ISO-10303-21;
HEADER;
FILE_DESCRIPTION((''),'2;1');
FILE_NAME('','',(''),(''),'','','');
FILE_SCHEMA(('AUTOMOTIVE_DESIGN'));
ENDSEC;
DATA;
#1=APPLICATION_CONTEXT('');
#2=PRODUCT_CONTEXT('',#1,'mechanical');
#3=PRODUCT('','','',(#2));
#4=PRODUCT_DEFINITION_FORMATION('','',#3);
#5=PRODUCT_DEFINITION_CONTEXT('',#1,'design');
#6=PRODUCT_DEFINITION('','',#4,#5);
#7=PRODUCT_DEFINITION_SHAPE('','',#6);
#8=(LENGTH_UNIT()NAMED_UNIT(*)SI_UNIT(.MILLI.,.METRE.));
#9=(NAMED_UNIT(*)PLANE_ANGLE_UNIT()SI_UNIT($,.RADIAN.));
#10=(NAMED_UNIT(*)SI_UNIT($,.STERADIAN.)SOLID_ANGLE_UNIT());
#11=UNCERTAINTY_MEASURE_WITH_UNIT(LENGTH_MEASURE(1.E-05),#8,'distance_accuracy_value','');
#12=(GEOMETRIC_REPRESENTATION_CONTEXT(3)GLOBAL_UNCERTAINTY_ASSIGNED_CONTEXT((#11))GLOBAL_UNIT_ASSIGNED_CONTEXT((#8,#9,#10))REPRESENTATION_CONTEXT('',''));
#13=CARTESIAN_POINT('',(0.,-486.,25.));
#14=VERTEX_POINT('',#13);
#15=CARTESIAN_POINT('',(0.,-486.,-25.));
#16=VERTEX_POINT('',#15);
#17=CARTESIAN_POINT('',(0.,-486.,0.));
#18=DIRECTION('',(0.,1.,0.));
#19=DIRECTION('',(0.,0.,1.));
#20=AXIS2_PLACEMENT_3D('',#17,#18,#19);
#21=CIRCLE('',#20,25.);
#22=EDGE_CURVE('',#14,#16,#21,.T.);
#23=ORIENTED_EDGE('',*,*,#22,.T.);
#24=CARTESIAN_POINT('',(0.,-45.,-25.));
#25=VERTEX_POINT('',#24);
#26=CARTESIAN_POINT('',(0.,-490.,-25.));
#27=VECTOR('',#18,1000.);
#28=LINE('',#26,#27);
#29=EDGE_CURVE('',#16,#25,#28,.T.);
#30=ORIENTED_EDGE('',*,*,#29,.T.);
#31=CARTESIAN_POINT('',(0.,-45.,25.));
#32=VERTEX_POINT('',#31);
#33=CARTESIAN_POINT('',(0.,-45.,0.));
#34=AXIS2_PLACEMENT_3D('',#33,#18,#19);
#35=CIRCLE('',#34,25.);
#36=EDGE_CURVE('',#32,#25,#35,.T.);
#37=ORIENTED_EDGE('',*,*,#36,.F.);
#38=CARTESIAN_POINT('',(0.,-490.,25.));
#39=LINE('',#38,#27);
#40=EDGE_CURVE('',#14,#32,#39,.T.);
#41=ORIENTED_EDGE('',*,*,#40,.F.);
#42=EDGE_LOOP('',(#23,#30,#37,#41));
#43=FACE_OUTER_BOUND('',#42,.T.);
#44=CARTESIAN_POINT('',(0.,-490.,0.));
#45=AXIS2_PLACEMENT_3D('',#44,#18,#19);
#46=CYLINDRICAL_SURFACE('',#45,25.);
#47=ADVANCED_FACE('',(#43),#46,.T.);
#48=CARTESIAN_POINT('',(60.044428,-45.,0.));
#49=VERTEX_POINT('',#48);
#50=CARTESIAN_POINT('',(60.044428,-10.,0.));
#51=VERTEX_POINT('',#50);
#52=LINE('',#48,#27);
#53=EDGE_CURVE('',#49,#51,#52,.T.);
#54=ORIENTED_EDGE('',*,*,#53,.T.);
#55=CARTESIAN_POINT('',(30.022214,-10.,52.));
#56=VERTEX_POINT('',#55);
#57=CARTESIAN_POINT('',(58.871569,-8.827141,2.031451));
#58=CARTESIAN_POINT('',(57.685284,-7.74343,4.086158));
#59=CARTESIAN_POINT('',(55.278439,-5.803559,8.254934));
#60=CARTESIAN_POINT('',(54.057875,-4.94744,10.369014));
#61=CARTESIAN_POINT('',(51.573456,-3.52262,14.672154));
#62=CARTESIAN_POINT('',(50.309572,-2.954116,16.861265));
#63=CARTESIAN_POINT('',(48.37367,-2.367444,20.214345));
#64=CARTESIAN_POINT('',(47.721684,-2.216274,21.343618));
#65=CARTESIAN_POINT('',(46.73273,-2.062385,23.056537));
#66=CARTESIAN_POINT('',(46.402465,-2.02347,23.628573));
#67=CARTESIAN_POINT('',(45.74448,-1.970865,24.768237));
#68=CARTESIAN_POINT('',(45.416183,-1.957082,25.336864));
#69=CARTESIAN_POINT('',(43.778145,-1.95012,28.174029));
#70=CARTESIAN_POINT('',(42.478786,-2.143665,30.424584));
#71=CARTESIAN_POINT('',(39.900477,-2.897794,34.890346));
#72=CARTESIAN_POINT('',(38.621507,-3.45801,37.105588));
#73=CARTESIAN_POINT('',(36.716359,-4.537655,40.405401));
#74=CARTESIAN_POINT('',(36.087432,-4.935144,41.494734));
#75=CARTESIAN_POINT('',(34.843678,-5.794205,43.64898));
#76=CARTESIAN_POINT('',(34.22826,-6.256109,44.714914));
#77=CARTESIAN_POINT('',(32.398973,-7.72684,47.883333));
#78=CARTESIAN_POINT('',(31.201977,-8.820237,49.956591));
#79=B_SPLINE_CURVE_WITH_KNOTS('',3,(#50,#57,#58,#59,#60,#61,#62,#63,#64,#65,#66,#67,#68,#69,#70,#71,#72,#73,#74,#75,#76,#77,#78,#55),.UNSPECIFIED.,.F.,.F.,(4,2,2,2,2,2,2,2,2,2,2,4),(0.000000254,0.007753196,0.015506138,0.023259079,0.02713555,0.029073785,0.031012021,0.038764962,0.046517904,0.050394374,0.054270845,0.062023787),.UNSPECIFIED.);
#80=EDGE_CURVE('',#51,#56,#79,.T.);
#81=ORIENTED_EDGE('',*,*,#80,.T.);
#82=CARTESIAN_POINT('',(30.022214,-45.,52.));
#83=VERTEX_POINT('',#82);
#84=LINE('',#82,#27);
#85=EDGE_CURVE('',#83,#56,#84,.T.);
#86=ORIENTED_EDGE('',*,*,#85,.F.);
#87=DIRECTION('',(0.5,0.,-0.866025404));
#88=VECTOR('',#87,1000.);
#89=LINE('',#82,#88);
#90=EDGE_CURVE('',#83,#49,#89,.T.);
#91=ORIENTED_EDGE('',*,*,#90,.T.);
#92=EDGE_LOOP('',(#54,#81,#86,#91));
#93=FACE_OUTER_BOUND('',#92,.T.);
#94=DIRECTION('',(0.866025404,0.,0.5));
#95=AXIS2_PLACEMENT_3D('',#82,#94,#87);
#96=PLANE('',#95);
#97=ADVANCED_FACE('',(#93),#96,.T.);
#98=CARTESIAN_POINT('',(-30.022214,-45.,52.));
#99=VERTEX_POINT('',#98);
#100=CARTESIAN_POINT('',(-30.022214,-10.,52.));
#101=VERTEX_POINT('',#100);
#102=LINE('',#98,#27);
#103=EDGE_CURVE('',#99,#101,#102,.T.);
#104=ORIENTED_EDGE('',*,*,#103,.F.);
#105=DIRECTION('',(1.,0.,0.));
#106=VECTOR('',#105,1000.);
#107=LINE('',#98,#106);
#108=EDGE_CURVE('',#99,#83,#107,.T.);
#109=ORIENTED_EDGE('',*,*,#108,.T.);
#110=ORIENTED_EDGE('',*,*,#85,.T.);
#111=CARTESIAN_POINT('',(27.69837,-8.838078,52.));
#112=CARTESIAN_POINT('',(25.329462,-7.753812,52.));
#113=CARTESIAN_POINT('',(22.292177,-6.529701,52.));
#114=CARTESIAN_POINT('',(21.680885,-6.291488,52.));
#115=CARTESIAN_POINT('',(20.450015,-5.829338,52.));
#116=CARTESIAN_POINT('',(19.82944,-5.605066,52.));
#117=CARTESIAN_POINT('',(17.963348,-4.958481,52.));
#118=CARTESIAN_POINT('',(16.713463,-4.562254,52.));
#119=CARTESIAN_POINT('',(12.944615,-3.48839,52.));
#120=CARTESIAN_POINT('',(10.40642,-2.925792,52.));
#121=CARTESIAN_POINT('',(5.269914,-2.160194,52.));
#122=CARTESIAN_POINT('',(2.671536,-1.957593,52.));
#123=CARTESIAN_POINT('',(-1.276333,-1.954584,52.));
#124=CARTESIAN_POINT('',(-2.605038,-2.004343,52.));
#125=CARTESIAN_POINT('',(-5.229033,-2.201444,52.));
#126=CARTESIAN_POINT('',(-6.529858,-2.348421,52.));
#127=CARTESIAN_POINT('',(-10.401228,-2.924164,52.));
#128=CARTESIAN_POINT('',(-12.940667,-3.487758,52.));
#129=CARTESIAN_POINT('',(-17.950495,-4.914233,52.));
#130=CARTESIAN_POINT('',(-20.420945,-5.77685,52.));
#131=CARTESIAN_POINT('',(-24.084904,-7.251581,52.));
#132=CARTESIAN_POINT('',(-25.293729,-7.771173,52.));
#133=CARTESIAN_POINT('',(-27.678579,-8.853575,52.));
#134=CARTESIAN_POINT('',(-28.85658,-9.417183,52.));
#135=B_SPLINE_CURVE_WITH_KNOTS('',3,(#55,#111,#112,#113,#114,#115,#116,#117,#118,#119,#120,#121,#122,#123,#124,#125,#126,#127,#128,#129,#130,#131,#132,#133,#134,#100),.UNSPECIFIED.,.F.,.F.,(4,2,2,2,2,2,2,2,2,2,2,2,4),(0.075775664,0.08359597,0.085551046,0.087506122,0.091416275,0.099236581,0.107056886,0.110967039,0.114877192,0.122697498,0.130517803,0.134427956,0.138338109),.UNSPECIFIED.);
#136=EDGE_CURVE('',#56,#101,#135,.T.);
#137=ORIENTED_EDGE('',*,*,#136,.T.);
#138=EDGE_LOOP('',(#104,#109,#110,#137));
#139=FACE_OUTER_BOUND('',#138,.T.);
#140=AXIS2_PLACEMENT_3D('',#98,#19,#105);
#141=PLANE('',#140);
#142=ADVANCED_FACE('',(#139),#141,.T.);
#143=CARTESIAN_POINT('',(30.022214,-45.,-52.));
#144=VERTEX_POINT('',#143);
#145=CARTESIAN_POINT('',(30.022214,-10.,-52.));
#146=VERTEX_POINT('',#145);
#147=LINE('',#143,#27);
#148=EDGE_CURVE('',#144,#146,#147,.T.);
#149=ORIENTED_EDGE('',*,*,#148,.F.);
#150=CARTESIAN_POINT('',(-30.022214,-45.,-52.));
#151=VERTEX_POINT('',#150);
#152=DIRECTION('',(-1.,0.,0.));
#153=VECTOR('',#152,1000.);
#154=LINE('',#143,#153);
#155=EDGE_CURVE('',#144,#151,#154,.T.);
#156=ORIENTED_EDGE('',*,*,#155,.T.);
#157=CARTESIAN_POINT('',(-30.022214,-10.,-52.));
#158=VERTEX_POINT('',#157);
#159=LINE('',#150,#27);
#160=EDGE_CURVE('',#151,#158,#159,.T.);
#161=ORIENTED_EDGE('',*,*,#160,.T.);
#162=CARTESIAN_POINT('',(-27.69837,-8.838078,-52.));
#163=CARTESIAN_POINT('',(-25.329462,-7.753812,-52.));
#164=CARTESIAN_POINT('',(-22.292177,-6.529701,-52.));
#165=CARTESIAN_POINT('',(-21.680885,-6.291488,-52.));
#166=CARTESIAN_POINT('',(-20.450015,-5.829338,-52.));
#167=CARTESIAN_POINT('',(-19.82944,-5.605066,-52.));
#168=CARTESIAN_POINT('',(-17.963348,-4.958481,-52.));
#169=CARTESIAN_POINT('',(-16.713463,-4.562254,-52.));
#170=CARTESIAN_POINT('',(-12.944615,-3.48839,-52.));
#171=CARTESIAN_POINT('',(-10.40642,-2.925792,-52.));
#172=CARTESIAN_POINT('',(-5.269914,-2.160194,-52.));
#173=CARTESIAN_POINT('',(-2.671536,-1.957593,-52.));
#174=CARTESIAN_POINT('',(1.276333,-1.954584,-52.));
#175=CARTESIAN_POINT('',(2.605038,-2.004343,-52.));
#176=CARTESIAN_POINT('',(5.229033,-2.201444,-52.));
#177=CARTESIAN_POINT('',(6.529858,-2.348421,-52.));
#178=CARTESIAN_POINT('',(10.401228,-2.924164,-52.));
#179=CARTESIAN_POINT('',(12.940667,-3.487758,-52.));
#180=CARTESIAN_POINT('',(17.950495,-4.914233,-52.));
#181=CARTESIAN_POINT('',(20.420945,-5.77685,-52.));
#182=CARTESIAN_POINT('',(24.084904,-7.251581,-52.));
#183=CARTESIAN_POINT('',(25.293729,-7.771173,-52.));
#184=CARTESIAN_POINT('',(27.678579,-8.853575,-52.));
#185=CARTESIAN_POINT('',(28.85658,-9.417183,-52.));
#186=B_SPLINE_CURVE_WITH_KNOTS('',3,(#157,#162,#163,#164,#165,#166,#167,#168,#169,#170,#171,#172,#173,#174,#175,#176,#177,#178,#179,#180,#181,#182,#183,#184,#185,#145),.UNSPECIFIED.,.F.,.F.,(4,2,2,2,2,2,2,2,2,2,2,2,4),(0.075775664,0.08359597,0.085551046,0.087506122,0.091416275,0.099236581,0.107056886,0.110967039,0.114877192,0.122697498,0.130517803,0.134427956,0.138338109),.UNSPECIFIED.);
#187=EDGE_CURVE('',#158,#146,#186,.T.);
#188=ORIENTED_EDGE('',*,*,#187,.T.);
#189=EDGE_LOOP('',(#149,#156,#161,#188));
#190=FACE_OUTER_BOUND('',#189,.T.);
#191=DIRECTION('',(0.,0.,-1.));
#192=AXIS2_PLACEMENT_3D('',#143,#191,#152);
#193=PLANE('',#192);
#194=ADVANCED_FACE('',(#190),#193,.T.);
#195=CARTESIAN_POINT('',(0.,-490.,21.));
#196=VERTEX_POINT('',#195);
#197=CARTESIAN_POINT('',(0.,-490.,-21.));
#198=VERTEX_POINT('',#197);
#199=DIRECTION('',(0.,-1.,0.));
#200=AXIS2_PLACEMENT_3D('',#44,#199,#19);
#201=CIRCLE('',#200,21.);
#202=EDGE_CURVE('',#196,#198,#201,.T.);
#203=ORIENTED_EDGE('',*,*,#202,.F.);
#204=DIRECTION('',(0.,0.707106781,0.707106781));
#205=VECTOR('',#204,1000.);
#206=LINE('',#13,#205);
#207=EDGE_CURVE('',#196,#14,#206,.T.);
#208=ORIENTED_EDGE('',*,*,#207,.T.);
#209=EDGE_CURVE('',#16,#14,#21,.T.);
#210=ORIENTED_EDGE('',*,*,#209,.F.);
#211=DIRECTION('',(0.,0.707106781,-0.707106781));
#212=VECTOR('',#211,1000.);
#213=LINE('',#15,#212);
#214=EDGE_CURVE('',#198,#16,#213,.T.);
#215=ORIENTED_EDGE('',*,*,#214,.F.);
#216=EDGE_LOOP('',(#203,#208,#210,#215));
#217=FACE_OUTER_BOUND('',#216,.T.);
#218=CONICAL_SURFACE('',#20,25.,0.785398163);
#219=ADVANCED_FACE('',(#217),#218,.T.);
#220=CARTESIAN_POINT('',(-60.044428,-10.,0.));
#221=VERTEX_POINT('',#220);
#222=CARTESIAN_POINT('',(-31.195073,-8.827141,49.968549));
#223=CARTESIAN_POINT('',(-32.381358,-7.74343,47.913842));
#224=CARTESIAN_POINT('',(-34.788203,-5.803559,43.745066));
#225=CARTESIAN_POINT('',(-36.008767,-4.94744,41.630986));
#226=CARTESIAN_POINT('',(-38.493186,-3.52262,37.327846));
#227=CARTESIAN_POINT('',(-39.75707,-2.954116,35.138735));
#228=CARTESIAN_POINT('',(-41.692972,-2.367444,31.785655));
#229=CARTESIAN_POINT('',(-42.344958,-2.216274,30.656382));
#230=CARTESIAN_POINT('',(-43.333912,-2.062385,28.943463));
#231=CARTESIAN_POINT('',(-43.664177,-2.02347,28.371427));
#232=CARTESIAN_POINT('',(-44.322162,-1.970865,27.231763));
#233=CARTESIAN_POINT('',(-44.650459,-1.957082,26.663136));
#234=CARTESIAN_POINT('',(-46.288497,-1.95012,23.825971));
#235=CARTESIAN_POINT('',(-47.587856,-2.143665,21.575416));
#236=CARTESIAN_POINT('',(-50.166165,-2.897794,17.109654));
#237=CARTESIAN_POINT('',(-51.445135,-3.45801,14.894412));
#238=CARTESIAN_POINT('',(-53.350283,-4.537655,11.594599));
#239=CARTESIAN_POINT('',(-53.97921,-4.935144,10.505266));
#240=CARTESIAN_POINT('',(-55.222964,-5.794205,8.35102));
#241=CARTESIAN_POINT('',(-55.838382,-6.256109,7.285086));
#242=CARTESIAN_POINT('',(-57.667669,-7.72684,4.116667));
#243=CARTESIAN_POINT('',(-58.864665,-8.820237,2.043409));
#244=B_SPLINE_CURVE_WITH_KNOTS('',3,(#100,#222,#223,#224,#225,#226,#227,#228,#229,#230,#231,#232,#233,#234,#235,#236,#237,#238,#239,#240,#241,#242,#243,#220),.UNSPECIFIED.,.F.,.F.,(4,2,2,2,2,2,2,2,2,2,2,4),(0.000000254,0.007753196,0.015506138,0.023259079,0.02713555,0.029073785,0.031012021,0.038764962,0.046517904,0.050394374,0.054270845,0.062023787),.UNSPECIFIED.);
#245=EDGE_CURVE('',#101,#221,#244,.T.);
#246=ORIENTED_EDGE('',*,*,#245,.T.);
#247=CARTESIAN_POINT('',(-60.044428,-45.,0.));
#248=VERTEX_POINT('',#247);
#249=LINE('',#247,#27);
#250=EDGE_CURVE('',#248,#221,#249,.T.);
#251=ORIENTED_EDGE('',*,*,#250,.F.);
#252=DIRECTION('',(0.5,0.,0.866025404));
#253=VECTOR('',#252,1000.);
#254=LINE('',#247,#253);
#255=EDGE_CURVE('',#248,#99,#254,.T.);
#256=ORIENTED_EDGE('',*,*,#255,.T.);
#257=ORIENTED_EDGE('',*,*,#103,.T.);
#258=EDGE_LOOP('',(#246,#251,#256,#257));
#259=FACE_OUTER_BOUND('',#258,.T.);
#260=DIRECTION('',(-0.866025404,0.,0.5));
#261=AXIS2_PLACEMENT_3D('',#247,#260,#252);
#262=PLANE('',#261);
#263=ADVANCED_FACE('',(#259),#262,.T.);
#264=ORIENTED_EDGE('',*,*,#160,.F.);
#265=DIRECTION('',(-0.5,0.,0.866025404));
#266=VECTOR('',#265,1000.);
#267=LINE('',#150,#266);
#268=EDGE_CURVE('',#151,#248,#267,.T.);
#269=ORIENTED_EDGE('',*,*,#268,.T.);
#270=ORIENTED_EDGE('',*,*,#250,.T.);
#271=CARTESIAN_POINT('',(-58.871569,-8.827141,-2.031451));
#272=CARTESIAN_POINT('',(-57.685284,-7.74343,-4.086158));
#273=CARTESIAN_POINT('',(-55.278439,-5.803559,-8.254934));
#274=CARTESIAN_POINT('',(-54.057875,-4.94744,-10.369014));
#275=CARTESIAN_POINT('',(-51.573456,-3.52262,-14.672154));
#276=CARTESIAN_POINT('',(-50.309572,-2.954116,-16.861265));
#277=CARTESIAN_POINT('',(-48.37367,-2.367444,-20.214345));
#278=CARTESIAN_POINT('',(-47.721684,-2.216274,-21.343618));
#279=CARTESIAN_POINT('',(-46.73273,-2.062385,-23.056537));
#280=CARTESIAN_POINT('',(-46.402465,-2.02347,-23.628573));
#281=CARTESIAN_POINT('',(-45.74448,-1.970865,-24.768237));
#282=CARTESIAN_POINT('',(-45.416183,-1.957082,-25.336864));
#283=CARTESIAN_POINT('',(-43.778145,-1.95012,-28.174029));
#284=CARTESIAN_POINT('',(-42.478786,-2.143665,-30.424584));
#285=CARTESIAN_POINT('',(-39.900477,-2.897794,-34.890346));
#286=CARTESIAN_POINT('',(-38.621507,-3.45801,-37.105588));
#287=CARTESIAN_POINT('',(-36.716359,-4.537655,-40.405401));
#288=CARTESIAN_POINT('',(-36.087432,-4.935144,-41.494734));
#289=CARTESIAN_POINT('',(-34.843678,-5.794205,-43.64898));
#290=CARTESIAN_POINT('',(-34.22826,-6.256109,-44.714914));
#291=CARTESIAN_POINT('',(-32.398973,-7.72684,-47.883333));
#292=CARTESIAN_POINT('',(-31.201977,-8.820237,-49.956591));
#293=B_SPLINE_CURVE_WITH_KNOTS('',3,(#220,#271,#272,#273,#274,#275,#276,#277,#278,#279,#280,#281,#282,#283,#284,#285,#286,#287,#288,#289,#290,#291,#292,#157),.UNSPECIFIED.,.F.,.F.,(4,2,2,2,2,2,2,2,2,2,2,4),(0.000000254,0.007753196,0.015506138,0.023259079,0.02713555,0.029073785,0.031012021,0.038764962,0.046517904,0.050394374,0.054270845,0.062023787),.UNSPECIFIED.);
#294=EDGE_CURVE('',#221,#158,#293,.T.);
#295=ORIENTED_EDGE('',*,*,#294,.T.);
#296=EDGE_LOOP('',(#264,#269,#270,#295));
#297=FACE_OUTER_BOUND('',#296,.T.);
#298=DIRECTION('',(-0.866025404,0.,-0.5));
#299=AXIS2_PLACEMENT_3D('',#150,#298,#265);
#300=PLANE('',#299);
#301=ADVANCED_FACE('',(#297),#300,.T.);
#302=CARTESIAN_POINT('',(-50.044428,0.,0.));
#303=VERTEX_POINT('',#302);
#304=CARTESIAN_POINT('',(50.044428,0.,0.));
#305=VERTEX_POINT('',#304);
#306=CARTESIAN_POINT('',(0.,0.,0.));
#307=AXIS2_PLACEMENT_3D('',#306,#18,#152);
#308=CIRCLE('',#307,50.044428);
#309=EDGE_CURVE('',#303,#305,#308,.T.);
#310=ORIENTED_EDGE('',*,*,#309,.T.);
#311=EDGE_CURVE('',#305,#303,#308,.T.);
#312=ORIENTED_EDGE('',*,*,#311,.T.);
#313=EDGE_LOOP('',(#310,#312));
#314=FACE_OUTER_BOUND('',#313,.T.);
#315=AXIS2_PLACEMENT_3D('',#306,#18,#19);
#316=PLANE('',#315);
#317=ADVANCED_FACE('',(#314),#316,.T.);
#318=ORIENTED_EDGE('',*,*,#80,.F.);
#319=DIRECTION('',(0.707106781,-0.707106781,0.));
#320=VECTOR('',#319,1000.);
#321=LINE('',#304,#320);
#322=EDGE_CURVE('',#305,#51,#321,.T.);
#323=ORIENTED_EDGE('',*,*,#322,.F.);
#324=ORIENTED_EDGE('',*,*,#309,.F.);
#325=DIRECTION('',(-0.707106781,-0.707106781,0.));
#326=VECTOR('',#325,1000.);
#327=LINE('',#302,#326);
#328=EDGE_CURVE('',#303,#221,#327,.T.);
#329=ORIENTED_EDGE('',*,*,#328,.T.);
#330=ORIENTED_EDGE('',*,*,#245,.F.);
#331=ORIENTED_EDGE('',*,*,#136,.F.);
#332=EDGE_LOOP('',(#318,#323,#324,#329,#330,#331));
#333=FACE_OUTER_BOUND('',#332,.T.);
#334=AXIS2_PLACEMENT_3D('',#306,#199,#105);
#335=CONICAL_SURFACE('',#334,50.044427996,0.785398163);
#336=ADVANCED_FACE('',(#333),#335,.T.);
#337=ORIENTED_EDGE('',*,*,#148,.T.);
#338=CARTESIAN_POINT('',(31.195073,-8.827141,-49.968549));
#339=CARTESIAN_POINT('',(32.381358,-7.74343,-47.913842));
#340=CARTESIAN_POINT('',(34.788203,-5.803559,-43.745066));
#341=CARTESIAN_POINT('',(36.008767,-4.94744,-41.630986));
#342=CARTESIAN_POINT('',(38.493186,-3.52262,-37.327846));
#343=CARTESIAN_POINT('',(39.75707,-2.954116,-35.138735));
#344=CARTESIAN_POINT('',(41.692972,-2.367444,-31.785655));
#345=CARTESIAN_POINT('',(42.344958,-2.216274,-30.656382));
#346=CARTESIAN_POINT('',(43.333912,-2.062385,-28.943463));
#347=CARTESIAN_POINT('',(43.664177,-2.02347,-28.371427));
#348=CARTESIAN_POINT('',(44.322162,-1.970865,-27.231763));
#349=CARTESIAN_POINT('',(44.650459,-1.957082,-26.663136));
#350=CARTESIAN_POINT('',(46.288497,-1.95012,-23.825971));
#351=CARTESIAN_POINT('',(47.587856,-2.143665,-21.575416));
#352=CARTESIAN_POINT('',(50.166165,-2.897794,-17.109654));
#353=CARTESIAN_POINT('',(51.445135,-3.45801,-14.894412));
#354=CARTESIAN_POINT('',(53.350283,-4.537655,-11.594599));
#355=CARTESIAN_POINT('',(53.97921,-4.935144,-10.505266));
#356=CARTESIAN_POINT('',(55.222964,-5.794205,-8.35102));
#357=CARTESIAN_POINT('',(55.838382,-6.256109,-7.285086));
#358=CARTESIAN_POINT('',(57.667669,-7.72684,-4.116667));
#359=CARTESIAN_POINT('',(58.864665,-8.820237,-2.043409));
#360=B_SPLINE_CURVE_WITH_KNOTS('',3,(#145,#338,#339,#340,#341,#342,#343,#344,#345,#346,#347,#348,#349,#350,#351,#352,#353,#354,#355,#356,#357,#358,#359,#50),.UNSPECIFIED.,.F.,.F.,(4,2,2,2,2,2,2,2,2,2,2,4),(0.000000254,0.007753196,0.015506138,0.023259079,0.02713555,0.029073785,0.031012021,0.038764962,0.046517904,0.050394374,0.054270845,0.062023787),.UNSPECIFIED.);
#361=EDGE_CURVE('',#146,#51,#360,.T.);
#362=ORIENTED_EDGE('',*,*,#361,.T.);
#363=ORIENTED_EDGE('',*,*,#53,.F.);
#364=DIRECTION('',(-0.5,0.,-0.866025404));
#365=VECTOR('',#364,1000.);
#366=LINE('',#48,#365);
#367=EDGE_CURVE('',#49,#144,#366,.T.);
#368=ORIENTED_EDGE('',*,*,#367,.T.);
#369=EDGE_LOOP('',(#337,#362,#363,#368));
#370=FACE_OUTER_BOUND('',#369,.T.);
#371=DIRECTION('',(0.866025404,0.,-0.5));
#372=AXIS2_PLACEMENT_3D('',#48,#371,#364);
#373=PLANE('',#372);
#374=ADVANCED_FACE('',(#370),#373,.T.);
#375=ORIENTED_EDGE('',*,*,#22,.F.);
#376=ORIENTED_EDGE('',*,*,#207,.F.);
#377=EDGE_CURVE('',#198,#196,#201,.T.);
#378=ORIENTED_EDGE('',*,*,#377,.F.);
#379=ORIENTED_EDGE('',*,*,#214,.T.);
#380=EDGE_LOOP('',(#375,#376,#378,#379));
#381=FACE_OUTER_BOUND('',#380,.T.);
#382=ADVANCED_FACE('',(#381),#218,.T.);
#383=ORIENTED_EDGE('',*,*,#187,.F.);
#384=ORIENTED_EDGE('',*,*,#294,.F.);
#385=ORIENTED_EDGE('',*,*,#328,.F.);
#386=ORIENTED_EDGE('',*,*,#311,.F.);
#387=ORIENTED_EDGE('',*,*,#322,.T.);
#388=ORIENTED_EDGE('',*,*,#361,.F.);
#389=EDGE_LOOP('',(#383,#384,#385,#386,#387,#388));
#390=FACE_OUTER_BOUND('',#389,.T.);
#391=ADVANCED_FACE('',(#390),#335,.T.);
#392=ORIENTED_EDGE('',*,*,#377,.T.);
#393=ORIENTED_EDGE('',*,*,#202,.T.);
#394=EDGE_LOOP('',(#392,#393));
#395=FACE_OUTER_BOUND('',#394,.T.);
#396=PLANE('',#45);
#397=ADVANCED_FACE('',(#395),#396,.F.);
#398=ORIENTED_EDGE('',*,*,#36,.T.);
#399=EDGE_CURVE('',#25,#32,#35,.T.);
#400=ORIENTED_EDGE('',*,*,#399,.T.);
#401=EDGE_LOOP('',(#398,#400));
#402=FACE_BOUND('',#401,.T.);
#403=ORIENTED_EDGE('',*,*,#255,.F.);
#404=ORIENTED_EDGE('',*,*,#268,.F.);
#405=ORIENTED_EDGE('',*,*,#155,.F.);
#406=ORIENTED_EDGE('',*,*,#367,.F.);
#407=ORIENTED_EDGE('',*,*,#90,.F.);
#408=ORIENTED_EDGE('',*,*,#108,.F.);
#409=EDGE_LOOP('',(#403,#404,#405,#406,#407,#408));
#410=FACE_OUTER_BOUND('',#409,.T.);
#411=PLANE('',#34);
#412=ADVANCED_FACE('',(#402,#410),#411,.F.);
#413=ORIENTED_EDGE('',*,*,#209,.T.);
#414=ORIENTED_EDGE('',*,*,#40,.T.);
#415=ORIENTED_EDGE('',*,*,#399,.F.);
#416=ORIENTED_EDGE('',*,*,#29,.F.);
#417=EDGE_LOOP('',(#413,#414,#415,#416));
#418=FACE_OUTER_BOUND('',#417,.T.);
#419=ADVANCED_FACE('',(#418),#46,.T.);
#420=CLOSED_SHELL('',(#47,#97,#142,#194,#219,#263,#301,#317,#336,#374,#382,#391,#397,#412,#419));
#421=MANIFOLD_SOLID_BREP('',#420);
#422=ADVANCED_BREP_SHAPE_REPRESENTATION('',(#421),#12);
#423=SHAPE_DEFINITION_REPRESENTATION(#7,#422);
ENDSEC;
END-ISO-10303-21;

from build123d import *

# Parameters (mm, degrees)
HEX_HEAD_DEPTH              = 45
SHANK_SKETCH_50_R           = 25
SHANK_50X490_DEPTH          = 490
SHANK_END_CHAMFER_4X45_SIZE = 4


with BuildPart() as part:
    # Hex Head Sketch AF104 → Hex Head (new body)
    with BuildSketch(Plane(origin=(0, 0, 0), x_dir=(1, 0, 0), z_dir=(0, 1, 0))):
        Polygon((60.044427996, 0), (30.022213998, 52), (-30.022213998, 52), (-60.044427996, 0), (-30.022213998, -52), (30.022213998, -52), align=None)
    extrude(amount=-HEX_HEAD_DEPTH)

    # Head Chamfer Profile → Head Corner Chamfer Cut (revolve, cut)
    with BuildSketch(Plane.XY, mode=Mode.PRIVATE) as head_corner_chamfer_cut_sk:
        Polygon((50.044427996, 0), (60.044427996, 0), (60.044427996, -10), align=None)
    revolve(head_corner_chamfer_cut_sk.sketch.rotate(Axis((0, 0, 0), (0, -1, 0)), 180.000000001), axis=Axis((0, 0, 0), (0, -1, 0)), mode=Mode.SUBTRACT)

    # Shank Sketch Ø50 → Shank Ø50x490 (add)
    with BuildSketch(Plane(origin=(0, 0, 0), x_dir=(1, 0, 0), z_dir=(0, 1, 0))):
        with Locations(Location((0, 0, 0), (0, 0, 270))):
            Circle(SHANK_SKETCH_50_R)
    extrude(amount=-SHANK_50X490_DEPTH)

    # Shank End Chamfer 4x45°
    shank_end_chamfer_4x45_edges = [part.edges().sort_by_distance(p)[0] for p in [
        (0, -490, -25),
    ]]
    chamfer(shank_end_chamfer_4x45_edges, length=SHANK_END_CHAMFER_4X45_SIZE)


solid = part.part
